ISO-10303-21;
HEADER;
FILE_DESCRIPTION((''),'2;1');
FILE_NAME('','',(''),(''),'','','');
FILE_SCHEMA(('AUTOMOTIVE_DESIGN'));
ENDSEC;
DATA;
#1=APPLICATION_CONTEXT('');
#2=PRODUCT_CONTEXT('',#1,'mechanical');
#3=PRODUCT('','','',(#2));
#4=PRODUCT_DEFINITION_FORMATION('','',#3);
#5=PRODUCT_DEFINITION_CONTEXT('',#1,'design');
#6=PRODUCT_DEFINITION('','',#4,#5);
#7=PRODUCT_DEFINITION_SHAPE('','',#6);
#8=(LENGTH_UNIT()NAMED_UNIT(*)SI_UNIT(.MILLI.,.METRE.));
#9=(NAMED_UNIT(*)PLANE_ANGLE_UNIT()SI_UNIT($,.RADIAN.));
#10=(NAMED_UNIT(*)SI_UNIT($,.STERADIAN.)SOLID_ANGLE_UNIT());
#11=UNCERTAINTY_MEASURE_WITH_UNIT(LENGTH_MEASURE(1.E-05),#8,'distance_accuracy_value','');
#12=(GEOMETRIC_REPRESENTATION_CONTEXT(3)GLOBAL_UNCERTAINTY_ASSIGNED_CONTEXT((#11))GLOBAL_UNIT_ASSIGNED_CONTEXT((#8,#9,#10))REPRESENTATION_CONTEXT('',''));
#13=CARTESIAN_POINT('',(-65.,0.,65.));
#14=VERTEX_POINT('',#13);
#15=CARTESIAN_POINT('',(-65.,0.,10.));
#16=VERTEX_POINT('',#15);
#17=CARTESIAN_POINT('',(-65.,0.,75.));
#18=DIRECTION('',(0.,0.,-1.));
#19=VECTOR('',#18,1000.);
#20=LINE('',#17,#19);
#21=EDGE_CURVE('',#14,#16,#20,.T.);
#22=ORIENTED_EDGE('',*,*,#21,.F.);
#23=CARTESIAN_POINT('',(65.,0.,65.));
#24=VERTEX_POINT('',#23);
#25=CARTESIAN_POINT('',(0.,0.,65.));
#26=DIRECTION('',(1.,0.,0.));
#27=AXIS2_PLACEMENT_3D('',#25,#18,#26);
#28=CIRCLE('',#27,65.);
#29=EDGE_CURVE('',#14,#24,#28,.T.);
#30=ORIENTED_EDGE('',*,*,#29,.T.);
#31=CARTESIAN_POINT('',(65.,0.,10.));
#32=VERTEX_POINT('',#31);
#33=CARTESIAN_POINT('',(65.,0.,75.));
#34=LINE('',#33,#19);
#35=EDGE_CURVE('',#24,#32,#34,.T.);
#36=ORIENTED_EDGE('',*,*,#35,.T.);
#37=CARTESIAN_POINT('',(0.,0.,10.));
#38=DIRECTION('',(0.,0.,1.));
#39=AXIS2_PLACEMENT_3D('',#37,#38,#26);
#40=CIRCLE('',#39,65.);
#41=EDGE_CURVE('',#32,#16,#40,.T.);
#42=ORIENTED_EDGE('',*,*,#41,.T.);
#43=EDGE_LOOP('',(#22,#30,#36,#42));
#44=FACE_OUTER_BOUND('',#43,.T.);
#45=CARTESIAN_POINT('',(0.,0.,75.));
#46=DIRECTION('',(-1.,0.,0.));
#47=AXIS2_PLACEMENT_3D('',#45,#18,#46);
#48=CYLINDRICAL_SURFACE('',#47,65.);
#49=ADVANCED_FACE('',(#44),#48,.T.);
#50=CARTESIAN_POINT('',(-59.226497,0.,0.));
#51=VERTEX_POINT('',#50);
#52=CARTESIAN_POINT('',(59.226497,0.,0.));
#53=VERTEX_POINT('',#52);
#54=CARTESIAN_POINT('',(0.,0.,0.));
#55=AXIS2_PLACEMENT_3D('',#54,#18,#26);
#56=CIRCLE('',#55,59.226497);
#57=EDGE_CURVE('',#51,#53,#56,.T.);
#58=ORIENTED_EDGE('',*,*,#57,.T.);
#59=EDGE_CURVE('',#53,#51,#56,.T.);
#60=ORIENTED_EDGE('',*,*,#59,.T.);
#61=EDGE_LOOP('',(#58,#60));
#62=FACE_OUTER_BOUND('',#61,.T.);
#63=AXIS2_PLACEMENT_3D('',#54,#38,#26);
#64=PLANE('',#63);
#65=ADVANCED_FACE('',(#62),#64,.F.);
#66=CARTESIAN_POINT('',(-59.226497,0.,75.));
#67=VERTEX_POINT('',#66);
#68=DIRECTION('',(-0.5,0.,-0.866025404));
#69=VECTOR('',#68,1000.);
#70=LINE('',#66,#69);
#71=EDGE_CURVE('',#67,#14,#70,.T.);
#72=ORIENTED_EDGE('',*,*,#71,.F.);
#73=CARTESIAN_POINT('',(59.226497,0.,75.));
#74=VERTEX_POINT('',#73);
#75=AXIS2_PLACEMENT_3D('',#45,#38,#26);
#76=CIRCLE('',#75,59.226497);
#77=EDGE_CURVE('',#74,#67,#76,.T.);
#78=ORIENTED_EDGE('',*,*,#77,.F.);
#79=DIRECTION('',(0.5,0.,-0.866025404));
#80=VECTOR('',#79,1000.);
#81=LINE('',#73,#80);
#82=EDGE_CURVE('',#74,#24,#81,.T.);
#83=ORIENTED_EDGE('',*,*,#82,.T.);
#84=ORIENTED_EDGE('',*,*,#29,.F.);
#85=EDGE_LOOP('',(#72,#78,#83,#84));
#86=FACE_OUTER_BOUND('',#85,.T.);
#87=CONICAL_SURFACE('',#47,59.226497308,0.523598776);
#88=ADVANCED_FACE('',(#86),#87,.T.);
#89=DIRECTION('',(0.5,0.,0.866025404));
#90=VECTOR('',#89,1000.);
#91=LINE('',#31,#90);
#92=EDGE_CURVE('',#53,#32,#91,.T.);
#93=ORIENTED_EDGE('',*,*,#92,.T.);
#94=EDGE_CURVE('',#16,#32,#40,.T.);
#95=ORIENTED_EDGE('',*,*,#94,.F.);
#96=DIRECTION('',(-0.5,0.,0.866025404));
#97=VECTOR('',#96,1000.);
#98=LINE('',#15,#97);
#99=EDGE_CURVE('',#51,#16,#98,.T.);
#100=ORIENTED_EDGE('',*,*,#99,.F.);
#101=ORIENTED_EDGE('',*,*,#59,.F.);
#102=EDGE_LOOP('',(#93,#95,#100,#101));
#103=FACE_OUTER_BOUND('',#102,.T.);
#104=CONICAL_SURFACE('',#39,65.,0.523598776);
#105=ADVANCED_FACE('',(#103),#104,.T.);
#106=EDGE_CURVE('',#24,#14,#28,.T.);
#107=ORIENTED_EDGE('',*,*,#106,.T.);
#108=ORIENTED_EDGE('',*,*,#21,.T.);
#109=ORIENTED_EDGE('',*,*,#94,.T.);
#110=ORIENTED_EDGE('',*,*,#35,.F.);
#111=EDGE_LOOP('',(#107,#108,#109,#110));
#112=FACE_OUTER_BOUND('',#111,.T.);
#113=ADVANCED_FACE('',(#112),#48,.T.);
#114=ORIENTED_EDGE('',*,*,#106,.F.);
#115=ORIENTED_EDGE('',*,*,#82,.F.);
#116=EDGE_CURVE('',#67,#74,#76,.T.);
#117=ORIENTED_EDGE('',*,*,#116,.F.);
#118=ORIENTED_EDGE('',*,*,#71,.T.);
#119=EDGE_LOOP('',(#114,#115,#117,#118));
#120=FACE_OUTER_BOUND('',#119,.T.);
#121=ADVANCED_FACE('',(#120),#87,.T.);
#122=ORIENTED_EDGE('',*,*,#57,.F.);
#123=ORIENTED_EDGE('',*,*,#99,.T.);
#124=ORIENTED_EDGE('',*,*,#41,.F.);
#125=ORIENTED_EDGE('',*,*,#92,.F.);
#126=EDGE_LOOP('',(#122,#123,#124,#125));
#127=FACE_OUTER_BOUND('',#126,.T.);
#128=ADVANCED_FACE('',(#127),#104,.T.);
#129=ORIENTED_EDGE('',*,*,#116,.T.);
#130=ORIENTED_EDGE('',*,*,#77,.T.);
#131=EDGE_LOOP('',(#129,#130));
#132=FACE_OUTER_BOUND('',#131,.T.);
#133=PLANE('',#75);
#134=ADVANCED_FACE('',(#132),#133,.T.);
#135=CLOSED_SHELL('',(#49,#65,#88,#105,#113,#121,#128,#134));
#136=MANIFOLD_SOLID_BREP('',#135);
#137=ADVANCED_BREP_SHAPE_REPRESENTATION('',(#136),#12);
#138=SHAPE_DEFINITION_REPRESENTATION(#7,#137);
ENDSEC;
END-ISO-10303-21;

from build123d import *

# Parameters (mm, degrees)
SKETCH_1_R      = 65
EXTRUDE_1_DEPTH = 75
CHAMFER_1_SIZE  = 10
CHAMFER_1_SIZE2 = 5.773502692


with BuildPart() as part:
    # 草图1 → 凸台-拉伸1 (new body)
    with BuildSketch(Plane.XY):
        Circle(SKETCH_1_R)
    extrude(amount=EXTRUDE_1_DEPTH)

    # 倒角1
    chamfer_1_edges = [part.edges().sort_by_distance(p)[0] for p in [
        (-65, 0, 0),
        (-65, 0, 75),
    ]]
    chamfer_1_side = [part.faces().sort_by_distance(p)[0] for p in [
        (-65, 0, 37.5),
    ]]
    chamfer(chamfer_1_edges, length=CHAMFER_1_SIZE, length2=CHAMFER_1_SIZE2, reference=chamfer_1_side[0])


solid = part.part
